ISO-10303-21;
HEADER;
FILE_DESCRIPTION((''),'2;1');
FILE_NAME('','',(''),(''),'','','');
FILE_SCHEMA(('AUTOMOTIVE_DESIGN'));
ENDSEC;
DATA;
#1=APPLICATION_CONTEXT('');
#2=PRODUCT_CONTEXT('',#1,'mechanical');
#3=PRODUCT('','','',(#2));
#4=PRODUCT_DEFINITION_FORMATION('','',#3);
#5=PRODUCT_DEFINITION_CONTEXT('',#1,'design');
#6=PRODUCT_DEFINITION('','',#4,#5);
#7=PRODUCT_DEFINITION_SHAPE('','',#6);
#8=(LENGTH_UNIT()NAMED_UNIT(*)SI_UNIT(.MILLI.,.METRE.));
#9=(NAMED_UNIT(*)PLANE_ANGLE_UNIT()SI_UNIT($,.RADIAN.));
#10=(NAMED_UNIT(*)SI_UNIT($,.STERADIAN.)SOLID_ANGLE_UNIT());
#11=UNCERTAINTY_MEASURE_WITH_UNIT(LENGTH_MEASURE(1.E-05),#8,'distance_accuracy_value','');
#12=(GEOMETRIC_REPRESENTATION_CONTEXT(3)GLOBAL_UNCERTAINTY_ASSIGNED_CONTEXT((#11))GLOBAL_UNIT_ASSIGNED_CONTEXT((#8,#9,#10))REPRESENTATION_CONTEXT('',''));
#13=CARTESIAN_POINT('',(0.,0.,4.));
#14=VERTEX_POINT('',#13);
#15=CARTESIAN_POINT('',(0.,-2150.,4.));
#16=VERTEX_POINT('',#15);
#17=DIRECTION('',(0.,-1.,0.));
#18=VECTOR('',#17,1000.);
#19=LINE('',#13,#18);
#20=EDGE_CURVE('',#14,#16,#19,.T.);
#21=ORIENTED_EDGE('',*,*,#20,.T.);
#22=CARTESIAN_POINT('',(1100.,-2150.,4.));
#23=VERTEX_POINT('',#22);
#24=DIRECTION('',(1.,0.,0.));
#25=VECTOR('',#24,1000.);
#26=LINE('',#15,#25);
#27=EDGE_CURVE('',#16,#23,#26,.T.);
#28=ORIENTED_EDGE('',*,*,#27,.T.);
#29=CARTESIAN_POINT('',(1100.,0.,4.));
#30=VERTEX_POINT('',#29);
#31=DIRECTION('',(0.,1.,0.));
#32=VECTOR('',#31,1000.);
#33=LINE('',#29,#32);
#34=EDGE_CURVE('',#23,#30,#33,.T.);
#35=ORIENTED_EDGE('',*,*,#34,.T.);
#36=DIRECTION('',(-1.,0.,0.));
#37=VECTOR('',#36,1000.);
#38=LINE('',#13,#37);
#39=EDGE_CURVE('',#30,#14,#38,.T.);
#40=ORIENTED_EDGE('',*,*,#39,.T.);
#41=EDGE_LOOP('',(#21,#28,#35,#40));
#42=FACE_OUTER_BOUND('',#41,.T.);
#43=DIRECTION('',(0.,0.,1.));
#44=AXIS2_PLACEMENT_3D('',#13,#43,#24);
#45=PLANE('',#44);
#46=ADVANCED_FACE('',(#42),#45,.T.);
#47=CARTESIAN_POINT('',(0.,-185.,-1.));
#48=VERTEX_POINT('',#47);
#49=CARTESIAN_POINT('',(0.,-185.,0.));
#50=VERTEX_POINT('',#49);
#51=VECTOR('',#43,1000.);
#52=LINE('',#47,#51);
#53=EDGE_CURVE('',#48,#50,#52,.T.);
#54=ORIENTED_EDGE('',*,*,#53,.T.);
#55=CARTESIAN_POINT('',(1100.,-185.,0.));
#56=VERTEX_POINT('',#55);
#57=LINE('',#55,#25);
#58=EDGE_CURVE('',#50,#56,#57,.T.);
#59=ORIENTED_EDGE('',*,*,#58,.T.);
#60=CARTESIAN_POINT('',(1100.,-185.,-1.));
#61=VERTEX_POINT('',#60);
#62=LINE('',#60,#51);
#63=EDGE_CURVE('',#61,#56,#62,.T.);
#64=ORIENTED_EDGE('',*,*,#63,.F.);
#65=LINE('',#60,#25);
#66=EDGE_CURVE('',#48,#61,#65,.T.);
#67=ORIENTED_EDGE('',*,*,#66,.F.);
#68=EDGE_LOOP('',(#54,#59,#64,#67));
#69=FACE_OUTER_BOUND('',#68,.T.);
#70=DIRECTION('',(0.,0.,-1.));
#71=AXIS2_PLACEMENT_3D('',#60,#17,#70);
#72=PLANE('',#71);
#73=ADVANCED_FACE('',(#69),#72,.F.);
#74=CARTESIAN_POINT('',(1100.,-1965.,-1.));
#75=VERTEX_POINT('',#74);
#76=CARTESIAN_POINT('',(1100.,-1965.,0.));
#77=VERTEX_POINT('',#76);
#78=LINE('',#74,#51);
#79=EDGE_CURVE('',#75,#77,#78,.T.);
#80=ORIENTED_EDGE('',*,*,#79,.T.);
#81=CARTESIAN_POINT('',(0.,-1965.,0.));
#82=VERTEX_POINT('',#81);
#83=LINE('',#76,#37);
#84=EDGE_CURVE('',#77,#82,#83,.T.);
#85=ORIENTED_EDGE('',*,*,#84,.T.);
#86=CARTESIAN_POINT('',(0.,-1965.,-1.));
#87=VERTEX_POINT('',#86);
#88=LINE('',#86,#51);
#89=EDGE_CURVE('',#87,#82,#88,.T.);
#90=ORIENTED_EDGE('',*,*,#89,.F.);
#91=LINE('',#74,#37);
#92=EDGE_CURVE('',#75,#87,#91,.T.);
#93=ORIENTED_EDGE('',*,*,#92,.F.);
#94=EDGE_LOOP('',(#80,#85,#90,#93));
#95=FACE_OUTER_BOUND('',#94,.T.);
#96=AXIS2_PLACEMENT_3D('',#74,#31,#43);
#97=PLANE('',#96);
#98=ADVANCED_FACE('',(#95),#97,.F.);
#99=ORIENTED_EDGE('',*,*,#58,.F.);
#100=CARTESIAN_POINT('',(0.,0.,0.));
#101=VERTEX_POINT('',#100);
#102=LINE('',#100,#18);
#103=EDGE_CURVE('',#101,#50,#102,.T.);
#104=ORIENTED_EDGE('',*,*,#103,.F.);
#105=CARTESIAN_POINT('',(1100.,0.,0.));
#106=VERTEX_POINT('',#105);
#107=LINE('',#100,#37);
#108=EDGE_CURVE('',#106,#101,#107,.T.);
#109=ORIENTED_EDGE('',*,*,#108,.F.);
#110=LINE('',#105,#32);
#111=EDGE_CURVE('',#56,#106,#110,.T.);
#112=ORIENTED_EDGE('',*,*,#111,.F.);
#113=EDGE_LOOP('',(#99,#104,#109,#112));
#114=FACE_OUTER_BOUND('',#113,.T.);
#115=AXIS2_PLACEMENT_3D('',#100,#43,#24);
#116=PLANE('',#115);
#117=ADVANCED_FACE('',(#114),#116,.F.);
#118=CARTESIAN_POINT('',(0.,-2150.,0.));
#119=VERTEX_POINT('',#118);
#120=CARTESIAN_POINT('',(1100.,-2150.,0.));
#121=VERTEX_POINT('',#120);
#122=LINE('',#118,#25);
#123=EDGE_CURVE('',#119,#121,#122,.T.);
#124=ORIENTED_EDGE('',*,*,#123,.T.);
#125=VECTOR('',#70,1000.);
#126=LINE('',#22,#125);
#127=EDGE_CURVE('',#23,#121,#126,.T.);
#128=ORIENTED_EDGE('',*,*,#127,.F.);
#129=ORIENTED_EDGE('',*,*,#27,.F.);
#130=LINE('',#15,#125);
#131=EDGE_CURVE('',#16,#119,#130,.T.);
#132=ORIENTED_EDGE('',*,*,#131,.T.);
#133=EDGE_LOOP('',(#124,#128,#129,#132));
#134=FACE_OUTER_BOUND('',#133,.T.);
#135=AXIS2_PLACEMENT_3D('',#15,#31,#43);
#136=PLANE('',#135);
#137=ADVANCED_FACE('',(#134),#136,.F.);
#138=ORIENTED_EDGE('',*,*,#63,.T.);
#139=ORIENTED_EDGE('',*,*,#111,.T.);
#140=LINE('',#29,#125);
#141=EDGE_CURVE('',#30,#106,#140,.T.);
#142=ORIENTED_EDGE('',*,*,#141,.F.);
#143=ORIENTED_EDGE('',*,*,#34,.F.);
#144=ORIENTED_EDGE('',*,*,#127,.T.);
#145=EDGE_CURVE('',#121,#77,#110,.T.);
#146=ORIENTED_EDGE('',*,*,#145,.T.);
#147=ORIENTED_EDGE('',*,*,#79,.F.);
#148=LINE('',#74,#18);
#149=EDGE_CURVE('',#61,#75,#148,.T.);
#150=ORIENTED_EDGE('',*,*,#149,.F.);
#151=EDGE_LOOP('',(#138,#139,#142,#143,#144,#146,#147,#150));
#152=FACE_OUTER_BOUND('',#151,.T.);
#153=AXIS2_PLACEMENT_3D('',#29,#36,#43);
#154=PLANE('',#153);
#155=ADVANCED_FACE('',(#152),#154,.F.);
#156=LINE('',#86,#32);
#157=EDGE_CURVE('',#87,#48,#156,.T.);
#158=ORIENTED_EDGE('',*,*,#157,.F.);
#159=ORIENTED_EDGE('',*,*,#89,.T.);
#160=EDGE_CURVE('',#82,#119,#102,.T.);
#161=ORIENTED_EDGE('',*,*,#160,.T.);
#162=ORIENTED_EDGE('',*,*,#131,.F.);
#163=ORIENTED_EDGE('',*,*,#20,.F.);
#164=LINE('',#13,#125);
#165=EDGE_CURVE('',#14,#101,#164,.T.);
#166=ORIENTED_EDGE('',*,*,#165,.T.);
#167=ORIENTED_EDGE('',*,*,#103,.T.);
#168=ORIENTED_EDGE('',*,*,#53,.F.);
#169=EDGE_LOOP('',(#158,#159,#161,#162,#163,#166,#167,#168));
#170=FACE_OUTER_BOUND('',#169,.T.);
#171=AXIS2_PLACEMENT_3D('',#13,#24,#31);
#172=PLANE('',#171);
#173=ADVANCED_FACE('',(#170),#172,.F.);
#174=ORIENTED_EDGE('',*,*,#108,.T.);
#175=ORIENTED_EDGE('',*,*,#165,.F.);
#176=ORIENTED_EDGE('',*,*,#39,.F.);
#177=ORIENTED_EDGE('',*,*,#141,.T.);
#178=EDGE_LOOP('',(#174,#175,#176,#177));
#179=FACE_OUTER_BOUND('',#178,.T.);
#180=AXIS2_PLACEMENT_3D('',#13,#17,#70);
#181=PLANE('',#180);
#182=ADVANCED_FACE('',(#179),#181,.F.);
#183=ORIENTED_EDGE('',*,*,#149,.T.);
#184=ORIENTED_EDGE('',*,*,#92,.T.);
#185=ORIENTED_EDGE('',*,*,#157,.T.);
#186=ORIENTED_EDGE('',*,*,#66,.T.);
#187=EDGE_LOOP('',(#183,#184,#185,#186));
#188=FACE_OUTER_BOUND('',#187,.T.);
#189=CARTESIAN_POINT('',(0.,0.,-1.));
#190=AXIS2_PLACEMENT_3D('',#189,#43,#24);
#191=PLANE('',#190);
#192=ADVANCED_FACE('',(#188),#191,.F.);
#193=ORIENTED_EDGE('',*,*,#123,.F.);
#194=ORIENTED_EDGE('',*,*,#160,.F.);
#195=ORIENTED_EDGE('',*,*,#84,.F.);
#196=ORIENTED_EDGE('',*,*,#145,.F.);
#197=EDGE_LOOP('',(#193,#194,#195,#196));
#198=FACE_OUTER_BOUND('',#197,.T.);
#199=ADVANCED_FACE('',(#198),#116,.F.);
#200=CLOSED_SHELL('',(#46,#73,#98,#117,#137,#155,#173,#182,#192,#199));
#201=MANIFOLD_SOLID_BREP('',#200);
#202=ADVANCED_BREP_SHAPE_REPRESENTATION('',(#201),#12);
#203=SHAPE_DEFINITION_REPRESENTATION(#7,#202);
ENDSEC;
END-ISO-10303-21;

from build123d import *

# Parameters (mm, degrees)
SKETCH_1_W      = 1100
SKETCH_1_H      = 2150
EXTRUDE_1_DEPTH = 4
SKETCH_2_W      = 1100
SKETCH_2_H      = 1780
EXTRUDE_2_DEPTH = 1


with BuildPart() as part:
    # 草图1 → 凸台-拉伸1 (new body)
    with BuildSketch(Plane.XY):
        with Locations((550, -1075)):
            Rectangle(SKETCH_1_W, SKETCH_1_H)
    extrude(amount=EXTRUDE_1_DEPTH)

    # 草图2 → 凸台-拉伸2 (add)
    with BuildSketch(Plane(origin=(0, 0, 0), x_dir=(-1, 0, 0), z_dir=(0, 0, -1))):
        with Locations((-550, -1075)):
            Rectangle(SKETCH_2_W, SKETCH_2_H)
    extrude(amount=EXTRUDE_2_DEPTH)


solid = part.part
